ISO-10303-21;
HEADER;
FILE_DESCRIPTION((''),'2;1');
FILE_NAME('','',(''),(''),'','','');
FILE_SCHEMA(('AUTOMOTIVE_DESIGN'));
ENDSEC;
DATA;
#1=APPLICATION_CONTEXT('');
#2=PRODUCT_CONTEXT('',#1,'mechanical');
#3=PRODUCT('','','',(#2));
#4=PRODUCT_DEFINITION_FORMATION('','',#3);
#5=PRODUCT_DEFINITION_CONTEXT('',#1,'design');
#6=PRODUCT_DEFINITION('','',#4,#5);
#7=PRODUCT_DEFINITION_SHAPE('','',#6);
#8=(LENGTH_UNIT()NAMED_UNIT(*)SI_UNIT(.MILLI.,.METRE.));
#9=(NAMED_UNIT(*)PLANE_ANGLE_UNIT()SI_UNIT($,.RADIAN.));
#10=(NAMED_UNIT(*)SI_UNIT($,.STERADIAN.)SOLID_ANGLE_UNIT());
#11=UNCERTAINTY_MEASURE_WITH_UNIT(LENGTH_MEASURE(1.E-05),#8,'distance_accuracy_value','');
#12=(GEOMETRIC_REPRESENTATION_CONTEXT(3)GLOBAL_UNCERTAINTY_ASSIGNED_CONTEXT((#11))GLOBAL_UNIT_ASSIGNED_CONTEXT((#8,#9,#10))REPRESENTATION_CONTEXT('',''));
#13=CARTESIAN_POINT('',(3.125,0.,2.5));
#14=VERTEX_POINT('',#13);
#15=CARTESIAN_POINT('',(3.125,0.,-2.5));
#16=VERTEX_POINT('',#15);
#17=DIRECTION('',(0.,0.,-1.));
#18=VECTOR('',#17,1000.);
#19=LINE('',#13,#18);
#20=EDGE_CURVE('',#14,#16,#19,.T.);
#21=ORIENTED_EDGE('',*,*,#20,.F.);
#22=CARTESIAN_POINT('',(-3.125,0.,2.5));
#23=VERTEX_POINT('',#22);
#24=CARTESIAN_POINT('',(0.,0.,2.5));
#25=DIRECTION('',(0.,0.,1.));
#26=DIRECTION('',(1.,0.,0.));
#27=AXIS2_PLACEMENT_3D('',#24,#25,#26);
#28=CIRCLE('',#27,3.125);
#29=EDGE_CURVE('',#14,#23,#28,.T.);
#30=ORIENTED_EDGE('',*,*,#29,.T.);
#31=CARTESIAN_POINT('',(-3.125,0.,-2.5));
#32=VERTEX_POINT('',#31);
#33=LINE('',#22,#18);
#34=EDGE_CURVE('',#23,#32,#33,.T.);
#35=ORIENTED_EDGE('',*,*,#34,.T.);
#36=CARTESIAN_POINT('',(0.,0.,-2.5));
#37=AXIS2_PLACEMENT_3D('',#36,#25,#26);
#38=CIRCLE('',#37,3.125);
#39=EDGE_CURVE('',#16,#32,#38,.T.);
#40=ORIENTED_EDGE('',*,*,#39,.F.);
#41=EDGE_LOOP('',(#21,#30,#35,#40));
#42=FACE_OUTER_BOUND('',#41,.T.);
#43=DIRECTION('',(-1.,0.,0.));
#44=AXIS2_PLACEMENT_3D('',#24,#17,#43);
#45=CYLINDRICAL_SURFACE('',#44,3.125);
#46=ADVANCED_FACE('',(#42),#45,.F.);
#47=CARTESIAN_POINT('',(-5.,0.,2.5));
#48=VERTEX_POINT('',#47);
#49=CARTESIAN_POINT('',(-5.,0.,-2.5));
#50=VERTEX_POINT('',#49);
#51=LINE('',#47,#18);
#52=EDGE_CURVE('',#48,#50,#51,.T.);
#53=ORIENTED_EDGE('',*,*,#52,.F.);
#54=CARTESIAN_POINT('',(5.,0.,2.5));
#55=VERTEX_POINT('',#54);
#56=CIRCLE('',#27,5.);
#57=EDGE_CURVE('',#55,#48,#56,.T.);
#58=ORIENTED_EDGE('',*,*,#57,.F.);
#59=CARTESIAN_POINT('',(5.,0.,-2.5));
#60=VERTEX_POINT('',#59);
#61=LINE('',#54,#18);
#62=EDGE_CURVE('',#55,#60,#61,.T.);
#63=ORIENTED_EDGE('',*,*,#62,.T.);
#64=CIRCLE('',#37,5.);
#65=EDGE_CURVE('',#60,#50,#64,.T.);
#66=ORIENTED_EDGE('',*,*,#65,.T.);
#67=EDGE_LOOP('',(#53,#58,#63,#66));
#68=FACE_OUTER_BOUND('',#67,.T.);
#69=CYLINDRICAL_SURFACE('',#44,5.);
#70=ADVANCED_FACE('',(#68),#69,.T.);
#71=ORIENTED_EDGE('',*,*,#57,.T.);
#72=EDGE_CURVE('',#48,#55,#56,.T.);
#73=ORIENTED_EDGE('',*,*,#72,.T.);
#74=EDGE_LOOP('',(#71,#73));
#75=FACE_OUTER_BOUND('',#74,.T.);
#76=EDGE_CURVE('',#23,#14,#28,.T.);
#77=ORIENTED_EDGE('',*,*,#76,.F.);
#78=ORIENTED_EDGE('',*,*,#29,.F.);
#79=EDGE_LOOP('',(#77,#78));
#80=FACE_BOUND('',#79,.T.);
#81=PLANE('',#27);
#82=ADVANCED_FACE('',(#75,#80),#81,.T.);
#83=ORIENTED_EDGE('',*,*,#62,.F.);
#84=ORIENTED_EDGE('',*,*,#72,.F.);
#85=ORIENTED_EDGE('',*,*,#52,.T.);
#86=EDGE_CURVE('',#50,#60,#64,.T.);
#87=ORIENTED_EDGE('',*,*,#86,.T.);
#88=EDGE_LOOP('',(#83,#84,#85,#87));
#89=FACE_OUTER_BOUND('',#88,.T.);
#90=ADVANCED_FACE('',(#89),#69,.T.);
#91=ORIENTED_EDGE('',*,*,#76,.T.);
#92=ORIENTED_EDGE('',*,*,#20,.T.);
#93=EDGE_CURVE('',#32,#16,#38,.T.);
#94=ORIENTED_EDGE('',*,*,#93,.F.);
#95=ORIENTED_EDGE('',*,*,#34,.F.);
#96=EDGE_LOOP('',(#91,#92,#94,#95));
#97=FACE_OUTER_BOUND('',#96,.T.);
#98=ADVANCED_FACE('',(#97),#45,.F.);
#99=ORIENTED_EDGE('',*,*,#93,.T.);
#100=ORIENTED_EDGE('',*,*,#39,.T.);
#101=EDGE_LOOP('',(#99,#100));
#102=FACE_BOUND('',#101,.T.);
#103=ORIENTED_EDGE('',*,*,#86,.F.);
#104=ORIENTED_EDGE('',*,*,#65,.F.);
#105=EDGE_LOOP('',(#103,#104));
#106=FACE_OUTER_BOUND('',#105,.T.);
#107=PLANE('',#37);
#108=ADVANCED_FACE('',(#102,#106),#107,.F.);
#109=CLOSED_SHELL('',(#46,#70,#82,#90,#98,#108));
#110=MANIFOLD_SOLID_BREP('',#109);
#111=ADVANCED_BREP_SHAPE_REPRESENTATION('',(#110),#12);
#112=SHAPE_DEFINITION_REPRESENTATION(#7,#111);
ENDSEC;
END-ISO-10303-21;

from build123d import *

# Parameters (mm, degrees)
BUSH_RING_PROFILE_10_X_6_25_R   = 5
BUSH_RING_PROFILE_10_X_6_25_R_2 = 3.125
BUSH_BODY_L5_DEPTH              = 2.5


with BuildPart() as part:
    # Bush Ring Profile Ø10 x Ø6.25 → Bush Body L5 (new, symmetric)
    with BuildSketch(Plane.XY):
        Circle(BUSH_RING_PROFILE_10_X_6_25_R)
        Circle(BUSH_RING_PROFILE_10_X_6_25_R_2, mode=Mode.SUBTRACT)
    extrude(amount=BUSH_BODY_L5_DEPTH, both=True)


solid = part.part
